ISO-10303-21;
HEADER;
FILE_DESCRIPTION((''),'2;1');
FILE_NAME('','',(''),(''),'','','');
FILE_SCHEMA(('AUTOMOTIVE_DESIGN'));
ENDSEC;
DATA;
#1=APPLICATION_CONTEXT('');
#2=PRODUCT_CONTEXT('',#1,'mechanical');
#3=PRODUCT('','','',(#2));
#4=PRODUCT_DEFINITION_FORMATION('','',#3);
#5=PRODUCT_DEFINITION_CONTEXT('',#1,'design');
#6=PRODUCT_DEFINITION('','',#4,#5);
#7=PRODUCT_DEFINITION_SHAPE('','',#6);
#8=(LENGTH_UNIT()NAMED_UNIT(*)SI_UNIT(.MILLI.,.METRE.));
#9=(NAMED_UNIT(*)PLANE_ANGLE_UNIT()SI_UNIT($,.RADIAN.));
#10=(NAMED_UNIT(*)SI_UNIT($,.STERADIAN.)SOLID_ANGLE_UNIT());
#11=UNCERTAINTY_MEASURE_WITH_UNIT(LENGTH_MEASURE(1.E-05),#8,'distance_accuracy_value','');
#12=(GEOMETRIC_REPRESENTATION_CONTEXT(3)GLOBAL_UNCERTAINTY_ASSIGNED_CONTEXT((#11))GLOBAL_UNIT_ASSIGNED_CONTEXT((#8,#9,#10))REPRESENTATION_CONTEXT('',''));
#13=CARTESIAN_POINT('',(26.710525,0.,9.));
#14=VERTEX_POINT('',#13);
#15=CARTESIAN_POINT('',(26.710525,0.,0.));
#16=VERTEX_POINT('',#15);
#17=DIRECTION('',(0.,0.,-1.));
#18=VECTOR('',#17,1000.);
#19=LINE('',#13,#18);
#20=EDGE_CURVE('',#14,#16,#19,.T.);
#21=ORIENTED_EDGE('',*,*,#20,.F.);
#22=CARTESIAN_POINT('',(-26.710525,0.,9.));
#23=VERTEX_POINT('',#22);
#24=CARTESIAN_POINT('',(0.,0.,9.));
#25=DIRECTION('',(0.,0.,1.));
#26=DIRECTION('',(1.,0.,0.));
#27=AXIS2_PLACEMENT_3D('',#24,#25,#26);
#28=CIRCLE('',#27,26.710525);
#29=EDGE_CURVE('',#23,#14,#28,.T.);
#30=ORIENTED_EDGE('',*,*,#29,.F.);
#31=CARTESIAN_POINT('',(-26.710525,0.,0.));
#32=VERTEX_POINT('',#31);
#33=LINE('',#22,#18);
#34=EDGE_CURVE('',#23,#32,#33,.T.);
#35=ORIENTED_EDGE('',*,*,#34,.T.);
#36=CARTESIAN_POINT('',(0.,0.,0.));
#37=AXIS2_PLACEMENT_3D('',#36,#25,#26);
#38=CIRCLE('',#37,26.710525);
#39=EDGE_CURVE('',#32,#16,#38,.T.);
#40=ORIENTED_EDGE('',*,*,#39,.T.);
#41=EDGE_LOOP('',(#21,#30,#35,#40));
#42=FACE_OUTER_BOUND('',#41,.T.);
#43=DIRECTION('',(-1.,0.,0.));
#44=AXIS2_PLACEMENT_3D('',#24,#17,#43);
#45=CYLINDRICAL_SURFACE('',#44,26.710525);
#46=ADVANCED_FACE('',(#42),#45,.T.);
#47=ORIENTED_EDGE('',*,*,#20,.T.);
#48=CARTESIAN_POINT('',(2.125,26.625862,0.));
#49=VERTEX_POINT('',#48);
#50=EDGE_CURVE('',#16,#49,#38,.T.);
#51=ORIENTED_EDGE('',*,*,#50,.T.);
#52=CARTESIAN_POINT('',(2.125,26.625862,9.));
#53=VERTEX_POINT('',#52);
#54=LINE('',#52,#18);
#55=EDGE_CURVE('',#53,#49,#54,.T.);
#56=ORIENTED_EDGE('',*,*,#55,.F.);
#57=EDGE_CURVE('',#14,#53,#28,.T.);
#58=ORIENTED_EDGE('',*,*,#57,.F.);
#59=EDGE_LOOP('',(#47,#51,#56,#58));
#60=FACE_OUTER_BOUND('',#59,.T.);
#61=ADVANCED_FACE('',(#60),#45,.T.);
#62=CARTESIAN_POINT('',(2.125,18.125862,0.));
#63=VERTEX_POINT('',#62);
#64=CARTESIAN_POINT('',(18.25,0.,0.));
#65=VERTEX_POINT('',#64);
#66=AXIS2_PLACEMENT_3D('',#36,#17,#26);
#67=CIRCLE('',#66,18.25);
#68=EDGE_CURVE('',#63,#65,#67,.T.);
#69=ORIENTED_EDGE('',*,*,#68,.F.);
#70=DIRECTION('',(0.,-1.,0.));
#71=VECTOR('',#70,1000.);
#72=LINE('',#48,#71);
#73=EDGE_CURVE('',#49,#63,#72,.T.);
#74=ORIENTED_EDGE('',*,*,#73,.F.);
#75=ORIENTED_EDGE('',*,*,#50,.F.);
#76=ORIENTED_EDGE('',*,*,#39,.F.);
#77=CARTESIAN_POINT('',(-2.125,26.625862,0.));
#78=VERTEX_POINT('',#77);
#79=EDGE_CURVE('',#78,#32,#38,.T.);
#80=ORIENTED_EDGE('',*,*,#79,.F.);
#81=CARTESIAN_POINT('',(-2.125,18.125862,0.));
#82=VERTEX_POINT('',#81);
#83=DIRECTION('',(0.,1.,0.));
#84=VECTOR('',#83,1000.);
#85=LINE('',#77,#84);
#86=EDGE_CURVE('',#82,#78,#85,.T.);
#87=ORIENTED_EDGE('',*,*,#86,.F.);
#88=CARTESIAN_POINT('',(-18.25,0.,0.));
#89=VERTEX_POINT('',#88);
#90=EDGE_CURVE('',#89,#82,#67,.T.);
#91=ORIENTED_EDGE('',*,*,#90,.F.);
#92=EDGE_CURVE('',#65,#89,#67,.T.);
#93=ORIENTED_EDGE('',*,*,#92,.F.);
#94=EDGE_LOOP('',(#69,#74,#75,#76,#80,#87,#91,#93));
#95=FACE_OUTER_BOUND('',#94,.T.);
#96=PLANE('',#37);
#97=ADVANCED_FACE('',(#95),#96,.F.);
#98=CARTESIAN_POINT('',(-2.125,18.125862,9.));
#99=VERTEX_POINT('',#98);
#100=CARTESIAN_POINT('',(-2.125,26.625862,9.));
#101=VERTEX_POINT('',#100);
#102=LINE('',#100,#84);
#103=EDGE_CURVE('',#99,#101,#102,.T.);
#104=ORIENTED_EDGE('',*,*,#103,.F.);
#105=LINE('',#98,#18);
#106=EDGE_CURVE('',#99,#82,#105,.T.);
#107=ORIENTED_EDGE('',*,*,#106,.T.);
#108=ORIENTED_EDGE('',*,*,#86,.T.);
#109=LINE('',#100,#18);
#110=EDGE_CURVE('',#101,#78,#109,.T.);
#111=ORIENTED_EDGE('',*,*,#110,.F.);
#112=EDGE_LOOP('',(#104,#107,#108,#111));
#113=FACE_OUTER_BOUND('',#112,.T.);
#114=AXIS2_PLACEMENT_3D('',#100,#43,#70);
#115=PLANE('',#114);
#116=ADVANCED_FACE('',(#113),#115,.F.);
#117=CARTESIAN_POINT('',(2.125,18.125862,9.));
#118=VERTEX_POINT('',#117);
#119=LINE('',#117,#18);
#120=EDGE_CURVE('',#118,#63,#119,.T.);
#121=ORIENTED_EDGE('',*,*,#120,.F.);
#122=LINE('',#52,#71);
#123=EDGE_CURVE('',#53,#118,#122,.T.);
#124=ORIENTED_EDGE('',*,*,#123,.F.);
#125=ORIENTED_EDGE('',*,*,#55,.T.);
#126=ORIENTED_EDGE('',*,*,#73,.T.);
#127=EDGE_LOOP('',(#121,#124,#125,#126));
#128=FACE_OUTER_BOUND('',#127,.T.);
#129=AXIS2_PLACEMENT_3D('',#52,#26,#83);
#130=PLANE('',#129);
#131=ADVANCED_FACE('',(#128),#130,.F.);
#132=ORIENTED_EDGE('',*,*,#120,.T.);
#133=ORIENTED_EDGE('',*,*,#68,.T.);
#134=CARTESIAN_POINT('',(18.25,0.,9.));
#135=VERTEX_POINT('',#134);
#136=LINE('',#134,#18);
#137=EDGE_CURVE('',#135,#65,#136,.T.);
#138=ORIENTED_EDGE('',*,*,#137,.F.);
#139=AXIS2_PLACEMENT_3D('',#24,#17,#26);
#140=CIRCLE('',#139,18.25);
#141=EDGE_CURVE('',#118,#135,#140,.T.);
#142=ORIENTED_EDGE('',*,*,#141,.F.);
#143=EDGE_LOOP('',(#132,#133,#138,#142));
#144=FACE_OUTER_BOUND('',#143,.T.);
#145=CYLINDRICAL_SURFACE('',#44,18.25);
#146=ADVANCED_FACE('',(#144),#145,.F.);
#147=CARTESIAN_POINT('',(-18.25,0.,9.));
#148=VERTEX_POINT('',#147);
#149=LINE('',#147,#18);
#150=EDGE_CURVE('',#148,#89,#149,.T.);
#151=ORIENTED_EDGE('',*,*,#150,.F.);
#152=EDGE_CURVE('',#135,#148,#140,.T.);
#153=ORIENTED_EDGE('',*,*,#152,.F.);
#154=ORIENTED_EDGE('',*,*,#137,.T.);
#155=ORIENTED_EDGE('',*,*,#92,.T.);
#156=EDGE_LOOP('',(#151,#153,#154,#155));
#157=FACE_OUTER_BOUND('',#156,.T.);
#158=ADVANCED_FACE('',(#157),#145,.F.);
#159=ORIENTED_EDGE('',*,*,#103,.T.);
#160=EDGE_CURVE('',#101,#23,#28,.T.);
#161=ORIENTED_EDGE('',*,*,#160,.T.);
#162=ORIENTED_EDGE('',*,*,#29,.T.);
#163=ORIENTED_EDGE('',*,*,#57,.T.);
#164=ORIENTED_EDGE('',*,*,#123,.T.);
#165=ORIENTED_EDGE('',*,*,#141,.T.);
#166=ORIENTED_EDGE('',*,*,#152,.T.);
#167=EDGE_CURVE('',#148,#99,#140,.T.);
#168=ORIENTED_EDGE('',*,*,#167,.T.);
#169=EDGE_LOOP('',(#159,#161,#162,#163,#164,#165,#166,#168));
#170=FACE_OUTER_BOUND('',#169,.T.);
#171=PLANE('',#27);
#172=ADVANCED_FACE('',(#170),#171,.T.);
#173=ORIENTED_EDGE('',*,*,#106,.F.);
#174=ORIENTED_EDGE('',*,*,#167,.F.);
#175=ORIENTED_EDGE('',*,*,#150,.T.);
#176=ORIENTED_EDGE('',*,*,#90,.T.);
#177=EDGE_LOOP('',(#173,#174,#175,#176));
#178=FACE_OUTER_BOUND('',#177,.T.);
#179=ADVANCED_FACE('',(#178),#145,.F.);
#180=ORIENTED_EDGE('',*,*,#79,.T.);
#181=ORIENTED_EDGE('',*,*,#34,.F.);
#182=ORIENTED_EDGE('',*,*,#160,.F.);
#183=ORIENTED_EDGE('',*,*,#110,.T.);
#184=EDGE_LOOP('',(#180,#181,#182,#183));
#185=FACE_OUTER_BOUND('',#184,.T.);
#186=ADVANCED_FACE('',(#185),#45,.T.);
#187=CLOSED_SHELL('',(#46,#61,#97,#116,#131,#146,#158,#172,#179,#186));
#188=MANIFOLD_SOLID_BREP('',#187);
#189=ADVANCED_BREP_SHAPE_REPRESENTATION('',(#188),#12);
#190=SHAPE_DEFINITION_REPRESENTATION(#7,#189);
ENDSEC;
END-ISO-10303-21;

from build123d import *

# Parameters (mm, degrees)
EXTRUDE_1_DEPTH = 9


with BuildPart() as part:
    # 草图1 → 拉伸1 (new body)
    with BuildSketch(Plane.XY):
        with BuildLine():
            Line((-2.125, 26.625862048), (-2.125, 18.125862048))
            ThreePointArc((-2.125, 18.125862048), (0, -18.25), (2.125, 18.125862048))
            Line((2.125, 18.125862048), (2.125, 26.625862048))
            ThreePointArc((2.125, 26.625862048), (0, -26.710525169), (-2.125, 26.625862048))
        make_face()
    extrude(amount=EXTRUDE_1_DEPTH)


solid = part.part
